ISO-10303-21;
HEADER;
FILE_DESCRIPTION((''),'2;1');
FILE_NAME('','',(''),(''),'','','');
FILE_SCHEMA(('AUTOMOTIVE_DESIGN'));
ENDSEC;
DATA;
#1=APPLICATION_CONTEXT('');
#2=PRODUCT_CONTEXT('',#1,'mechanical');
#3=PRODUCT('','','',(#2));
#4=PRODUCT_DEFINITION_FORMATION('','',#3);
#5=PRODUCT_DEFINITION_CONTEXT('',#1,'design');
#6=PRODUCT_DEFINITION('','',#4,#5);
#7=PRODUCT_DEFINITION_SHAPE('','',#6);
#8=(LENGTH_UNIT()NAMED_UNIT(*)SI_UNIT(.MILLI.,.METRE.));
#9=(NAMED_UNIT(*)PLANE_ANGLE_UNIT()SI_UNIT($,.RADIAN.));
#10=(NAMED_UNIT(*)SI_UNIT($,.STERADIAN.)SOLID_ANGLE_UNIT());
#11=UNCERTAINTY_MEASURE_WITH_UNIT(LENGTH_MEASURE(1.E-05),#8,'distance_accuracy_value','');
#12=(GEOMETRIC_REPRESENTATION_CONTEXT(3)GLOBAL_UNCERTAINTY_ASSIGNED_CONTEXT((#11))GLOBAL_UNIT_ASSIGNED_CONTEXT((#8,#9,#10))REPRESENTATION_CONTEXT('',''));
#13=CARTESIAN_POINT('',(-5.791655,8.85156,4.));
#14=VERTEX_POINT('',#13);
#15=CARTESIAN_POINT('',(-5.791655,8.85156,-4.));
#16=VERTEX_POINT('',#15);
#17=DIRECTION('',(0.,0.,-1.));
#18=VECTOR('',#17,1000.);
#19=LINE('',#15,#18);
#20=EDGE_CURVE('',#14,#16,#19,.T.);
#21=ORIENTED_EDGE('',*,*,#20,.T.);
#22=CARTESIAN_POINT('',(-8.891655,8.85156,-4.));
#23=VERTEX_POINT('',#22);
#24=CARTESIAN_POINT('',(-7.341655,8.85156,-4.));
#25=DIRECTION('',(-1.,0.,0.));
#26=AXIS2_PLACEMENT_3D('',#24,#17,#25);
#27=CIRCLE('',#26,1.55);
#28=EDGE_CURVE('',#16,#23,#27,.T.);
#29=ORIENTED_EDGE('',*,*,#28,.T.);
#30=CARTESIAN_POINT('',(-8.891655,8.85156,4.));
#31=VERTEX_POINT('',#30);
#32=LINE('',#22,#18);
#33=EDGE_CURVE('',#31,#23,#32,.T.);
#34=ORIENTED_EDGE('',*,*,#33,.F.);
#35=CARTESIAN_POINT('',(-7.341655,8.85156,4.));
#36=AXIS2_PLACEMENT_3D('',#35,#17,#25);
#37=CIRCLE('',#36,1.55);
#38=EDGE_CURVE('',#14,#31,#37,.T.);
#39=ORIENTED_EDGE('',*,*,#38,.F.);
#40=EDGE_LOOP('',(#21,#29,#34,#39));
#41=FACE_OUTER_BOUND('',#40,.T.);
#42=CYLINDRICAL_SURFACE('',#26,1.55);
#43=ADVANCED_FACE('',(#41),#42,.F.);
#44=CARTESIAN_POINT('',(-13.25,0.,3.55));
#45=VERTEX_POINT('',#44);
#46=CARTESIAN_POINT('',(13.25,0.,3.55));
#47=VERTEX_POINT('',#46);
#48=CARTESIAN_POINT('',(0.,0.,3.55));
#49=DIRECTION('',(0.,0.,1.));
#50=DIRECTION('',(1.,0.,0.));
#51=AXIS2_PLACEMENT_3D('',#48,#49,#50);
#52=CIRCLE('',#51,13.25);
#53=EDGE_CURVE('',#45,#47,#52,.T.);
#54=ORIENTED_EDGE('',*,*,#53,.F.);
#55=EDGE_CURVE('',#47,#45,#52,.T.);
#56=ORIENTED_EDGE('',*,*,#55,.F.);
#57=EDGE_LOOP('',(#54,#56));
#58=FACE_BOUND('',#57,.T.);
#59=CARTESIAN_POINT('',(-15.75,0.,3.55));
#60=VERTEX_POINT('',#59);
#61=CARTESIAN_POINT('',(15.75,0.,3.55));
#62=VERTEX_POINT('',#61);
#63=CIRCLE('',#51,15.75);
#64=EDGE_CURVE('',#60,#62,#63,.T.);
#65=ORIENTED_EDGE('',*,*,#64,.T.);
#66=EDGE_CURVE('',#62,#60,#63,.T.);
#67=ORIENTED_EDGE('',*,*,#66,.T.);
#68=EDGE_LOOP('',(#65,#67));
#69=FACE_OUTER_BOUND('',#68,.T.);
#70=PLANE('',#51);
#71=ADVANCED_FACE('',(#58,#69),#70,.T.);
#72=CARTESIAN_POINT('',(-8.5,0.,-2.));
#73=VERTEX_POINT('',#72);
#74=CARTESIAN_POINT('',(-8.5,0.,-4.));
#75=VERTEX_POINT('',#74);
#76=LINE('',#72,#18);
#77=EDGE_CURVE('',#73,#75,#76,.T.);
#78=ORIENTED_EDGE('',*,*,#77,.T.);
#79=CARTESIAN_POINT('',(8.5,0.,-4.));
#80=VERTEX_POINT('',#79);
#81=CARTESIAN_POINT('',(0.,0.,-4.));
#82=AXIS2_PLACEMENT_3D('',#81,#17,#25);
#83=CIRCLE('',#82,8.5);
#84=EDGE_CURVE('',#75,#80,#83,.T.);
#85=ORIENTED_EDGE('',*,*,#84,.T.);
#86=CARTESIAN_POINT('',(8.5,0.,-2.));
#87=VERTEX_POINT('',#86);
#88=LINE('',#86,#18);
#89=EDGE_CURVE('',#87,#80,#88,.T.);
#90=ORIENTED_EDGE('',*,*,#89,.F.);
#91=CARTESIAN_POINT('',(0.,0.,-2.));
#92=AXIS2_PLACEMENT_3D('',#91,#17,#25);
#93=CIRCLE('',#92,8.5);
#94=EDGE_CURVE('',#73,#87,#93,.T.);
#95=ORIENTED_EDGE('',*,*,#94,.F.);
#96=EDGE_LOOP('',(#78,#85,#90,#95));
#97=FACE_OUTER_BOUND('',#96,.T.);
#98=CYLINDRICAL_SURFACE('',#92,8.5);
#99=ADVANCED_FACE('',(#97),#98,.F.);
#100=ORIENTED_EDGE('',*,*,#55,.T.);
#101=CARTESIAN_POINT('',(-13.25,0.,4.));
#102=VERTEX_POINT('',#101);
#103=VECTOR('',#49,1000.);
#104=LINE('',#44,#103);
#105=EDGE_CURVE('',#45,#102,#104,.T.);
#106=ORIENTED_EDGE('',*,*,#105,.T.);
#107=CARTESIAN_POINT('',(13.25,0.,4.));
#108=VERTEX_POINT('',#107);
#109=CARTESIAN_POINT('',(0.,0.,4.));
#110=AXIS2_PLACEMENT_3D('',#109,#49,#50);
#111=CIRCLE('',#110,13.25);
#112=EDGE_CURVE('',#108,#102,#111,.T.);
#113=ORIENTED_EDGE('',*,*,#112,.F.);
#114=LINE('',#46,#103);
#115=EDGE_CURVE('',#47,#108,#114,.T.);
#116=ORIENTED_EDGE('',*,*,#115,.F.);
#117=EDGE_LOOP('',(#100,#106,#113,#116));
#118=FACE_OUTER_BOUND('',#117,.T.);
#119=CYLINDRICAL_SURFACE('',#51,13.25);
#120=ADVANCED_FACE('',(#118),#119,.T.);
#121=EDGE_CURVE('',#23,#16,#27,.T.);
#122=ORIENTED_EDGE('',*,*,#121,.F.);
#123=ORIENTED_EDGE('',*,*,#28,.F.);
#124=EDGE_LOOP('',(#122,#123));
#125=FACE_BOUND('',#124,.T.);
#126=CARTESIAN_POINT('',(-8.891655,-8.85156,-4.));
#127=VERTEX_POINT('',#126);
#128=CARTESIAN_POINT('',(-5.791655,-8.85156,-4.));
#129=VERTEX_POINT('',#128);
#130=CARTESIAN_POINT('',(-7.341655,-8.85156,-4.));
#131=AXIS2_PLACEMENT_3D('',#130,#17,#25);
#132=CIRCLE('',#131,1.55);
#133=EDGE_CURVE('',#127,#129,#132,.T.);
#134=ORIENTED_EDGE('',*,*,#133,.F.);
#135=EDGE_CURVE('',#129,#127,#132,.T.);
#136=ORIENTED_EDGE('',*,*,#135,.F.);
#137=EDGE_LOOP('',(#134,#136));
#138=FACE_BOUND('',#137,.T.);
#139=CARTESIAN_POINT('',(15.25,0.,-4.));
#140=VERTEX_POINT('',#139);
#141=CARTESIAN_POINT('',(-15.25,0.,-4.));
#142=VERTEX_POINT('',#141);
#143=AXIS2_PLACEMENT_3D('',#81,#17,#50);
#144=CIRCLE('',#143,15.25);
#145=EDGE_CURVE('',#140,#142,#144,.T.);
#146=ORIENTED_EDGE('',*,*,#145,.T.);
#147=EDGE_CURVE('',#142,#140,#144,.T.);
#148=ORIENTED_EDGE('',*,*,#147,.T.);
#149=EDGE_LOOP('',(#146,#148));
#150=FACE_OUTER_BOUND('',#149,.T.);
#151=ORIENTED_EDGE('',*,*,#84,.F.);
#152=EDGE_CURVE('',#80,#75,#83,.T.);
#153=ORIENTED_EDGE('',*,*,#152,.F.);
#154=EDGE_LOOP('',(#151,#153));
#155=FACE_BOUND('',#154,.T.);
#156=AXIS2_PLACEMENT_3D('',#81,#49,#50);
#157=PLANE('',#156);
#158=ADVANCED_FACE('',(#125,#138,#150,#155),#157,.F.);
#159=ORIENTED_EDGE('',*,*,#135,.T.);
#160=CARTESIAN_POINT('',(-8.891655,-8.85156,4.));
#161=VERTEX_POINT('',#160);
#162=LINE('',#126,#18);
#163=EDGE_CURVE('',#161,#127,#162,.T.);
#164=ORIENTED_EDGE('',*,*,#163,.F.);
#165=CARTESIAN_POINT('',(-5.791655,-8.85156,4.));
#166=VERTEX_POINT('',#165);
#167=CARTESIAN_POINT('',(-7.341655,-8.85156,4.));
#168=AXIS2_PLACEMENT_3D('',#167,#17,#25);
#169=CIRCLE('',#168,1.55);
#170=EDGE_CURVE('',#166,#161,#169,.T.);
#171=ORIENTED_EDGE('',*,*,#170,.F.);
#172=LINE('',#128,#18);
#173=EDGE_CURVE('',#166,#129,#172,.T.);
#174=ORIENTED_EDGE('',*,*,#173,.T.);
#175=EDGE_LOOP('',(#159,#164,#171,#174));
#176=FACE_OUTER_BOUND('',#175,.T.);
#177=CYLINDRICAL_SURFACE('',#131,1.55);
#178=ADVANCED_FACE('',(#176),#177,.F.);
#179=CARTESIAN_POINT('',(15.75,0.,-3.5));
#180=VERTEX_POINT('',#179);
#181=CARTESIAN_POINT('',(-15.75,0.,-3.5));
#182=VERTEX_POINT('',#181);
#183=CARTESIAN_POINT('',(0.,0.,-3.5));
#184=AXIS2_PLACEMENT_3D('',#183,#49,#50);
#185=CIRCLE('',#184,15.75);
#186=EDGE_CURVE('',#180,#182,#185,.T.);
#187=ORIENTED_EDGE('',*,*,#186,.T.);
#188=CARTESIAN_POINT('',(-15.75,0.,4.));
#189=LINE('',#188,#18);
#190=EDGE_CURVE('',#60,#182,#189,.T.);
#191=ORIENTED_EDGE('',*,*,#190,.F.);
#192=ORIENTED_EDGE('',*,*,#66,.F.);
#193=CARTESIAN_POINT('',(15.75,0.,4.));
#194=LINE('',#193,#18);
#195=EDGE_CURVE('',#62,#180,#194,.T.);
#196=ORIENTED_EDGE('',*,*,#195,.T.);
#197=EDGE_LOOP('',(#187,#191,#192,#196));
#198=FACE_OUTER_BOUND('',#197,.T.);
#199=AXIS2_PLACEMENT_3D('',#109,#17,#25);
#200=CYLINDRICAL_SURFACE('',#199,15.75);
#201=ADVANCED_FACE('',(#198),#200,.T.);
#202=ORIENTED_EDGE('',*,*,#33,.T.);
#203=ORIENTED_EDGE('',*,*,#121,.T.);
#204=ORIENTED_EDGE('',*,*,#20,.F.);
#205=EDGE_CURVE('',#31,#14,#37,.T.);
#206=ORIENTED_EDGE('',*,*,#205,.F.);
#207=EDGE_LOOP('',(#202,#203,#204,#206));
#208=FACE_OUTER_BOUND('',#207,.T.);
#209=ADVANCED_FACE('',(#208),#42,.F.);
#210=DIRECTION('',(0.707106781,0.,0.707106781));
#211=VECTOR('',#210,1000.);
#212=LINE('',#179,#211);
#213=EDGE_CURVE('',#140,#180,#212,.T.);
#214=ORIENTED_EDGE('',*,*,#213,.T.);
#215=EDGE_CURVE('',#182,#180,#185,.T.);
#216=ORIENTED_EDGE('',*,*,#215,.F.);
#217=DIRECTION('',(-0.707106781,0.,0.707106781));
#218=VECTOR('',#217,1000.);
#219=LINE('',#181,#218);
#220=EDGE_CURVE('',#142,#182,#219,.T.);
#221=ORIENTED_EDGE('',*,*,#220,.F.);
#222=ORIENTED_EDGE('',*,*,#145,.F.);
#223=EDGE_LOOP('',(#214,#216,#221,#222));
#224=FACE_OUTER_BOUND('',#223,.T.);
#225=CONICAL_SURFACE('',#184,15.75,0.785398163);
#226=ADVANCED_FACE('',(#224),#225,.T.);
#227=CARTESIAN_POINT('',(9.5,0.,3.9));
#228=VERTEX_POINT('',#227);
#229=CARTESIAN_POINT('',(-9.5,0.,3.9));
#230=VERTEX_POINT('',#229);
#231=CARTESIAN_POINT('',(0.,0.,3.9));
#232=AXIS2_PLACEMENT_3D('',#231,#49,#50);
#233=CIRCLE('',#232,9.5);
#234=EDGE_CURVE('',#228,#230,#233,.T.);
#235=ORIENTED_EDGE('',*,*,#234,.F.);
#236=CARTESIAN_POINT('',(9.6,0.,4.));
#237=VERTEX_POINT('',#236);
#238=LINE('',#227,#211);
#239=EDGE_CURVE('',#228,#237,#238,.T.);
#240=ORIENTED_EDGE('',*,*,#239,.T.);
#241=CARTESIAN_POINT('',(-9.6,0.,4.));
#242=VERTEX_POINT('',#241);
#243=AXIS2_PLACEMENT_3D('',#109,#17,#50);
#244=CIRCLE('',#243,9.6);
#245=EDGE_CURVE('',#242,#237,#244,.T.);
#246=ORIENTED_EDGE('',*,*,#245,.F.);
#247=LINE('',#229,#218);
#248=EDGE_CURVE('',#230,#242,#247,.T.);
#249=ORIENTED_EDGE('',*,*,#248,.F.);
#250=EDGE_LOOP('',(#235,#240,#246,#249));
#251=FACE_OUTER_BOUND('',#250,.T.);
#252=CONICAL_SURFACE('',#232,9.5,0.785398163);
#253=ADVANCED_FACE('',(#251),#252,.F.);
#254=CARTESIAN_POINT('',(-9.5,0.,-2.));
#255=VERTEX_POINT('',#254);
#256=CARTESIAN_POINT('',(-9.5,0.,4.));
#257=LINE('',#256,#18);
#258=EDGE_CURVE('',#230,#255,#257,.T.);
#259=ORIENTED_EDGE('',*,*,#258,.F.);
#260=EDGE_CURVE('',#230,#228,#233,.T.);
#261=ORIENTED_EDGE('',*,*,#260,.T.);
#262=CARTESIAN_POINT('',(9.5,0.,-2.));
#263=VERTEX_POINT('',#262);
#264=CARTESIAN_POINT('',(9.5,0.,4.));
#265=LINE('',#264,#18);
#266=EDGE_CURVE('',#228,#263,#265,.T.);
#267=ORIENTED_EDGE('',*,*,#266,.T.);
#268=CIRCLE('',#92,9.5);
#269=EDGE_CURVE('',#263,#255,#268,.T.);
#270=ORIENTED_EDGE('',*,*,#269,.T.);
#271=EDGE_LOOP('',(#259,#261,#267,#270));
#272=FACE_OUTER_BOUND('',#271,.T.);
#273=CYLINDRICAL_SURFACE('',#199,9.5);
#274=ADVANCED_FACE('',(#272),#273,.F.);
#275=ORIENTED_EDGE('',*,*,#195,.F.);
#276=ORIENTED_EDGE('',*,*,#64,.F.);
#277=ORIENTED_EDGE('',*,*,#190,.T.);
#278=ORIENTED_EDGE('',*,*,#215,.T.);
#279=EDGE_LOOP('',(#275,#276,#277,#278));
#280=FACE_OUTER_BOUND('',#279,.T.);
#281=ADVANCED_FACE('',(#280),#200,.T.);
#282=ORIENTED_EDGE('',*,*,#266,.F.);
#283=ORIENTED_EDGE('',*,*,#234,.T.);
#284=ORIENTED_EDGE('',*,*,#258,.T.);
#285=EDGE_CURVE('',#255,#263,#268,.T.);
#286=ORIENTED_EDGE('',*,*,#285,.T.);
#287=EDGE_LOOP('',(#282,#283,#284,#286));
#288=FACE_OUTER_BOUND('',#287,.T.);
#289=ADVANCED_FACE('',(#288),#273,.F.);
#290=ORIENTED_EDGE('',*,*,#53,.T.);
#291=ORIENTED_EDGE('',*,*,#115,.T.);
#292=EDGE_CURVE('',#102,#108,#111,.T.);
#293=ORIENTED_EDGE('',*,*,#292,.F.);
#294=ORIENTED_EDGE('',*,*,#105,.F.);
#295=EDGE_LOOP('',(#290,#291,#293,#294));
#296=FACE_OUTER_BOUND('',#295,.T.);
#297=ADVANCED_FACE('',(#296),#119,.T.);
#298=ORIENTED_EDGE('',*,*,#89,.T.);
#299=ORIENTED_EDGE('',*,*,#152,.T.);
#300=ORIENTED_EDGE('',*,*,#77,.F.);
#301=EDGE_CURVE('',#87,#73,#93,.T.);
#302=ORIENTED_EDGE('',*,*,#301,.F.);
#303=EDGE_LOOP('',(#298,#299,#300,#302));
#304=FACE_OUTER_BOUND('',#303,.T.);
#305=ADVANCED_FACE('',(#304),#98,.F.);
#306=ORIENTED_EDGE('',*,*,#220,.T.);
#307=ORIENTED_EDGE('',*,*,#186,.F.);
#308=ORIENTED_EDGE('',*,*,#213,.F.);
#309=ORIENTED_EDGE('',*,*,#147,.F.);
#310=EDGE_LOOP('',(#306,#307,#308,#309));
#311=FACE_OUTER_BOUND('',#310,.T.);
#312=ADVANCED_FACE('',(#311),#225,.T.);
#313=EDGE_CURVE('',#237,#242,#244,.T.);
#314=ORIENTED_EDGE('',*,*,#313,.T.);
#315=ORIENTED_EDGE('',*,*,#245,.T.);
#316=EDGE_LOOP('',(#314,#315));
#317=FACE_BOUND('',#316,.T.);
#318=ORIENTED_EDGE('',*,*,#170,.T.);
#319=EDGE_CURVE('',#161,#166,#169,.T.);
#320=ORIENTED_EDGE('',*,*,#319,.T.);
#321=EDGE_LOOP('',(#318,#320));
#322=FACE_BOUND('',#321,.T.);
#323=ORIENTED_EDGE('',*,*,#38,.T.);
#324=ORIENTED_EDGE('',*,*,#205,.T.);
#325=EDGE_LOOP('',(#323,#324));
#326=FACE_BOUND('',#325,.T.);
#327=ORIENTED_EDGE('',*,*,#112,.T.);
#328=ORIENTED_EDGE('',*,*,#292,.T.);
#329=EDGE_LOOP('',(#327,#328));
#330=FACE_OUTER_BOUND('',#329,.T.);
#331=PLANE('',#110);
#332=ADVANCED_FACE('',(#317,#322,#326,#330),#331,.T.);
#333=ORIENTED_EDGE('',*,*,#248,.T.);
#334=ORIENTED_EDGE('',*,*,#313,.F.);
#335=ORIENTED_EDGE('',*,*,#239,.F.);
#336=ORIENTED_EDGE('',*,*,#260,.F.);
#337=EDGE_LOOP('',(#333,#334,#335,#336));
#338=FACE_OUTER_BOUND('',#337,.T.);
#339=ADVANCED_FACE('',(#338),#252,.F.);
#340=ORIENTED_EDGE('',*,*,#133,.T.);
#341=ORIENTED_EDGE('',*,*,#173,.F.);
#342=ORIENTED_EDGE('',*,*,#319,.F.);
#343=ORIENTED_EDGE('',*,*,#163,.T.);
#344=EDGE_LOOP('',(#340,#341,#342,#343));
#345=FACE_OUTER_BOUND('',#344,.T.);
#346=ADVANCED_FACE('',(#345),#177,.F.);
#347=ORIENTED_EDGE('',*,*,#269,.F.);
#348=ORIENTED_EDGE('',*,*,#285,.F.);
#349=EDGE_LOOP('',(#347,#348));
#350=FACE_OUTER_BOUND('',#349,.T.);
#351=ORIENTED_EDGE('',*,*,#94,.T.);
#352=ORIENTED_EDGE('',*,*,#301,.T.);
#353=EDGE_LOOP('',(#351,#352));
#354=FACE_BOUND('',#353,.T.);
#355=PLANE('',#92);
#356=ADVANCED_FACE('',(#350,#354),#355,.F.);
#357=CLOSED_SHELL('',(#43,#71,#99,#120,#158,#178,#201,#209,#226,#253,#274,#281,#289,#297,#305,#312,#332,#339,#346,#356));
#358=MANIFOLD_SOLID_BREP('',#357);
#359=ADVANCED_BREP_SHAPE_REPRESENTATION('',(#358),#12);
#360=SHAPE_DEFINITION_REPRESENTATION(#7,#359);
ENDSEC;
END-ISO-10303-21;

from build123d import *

# Parameters (mm, degrees)
SKETCH1_R                  = 15.75
SKETCH1_R_2                = 9.5
BOSS_EXTRUDE1_DEPTH        = 4
SKETCH3_R                  = 10.639095477
SKETCH3_R_2                = 8.5
BOSS_EXTRUDE2_DEPTH        = 2
F_3_1_3_1_DIAMETER_HOLE1_D = 3.1
SKETCH7_R                  = 18.245705154
SKETCH7_R_2                = 13.25
CUT_EXTRUDE1_DEPTH         = 0.45
CHAMFER1_SIZE              = 0.5
CHAMFER2_SIZE              = 0.1


with BuildPart() as part:
    # Sketch1 → Boss-Extrude1 (new, symmetric)
    with BuildSketch(Plane.XY):
        Circle(SKETCH1_R)
        Circle(SKETCH1_R_2, mode=Mode.SUBTRACT)
    extrude(amount=BOSS_EXTRUDE1_DEPTH, both=True)

    # Sketch3 → Boss-Extrude2 (add)
    with BuildSketch(Plane(origin=(0, 0, -4), x_dir=(-1, 0, 0), z_dir=(0, 0, -1))):
        Circle(SKETCH3_R)
        Circle(SKETCH3_R_2, mode=Mode.SUBTRACT)
    extrude(amount=-BOSS_EXTRUDE2_DEPTH)

    # Ø3.1 (3.1) Diameter Hole1 (through all)
    with Locations(Plane(origin=(0, 0, -4), x_dir=(-1, 0, 0), z_dir=(0, 0, -1))):
        with Locations((7.341654592, 8.851559628)):
            f_3_1_3_1_diameter_hole1 = Hole(F_3_1_3_1_DIAMETER_HOLE1_D / 2)

    # Mirror1: Ø3.1 (3.1) Diameter Hole1 across plane
    add(f_3_1_3_1_diameter_hole1.mirror(Plane.ZX), mode=Mode.SUBTRACT)

    # Sketch7 → Cut-Extrude1 (cut)
    with BuildSketch(Plane.XY.offset(4)):
        Circle(SKETCH7_R)
        Circle(SKETCH7_R_2, mode=Mode.SUBTRACT)
    extrude(amount=-CUT_EXTRUDE1_DEPTH, mode=Mode.SUBTRACT)

    # Chamfer1
    chamfer1_edges = [part.edges().sort_by_distance(p)[0] for p in [
        (-15.75, 0, -4),
    ]]
    chamfer(chamfer1_edges, length=CHAMFER1_SIZE)

    # Chamfer2
    chamfer2_edges = [part.edges().sort_by_distance(p)[0] for p in [
        (-9.5, 0, 4),
    ]]
    chamfer(chamfer2_edges, length=CHAMFER2_SIZE)


solid = part.part
